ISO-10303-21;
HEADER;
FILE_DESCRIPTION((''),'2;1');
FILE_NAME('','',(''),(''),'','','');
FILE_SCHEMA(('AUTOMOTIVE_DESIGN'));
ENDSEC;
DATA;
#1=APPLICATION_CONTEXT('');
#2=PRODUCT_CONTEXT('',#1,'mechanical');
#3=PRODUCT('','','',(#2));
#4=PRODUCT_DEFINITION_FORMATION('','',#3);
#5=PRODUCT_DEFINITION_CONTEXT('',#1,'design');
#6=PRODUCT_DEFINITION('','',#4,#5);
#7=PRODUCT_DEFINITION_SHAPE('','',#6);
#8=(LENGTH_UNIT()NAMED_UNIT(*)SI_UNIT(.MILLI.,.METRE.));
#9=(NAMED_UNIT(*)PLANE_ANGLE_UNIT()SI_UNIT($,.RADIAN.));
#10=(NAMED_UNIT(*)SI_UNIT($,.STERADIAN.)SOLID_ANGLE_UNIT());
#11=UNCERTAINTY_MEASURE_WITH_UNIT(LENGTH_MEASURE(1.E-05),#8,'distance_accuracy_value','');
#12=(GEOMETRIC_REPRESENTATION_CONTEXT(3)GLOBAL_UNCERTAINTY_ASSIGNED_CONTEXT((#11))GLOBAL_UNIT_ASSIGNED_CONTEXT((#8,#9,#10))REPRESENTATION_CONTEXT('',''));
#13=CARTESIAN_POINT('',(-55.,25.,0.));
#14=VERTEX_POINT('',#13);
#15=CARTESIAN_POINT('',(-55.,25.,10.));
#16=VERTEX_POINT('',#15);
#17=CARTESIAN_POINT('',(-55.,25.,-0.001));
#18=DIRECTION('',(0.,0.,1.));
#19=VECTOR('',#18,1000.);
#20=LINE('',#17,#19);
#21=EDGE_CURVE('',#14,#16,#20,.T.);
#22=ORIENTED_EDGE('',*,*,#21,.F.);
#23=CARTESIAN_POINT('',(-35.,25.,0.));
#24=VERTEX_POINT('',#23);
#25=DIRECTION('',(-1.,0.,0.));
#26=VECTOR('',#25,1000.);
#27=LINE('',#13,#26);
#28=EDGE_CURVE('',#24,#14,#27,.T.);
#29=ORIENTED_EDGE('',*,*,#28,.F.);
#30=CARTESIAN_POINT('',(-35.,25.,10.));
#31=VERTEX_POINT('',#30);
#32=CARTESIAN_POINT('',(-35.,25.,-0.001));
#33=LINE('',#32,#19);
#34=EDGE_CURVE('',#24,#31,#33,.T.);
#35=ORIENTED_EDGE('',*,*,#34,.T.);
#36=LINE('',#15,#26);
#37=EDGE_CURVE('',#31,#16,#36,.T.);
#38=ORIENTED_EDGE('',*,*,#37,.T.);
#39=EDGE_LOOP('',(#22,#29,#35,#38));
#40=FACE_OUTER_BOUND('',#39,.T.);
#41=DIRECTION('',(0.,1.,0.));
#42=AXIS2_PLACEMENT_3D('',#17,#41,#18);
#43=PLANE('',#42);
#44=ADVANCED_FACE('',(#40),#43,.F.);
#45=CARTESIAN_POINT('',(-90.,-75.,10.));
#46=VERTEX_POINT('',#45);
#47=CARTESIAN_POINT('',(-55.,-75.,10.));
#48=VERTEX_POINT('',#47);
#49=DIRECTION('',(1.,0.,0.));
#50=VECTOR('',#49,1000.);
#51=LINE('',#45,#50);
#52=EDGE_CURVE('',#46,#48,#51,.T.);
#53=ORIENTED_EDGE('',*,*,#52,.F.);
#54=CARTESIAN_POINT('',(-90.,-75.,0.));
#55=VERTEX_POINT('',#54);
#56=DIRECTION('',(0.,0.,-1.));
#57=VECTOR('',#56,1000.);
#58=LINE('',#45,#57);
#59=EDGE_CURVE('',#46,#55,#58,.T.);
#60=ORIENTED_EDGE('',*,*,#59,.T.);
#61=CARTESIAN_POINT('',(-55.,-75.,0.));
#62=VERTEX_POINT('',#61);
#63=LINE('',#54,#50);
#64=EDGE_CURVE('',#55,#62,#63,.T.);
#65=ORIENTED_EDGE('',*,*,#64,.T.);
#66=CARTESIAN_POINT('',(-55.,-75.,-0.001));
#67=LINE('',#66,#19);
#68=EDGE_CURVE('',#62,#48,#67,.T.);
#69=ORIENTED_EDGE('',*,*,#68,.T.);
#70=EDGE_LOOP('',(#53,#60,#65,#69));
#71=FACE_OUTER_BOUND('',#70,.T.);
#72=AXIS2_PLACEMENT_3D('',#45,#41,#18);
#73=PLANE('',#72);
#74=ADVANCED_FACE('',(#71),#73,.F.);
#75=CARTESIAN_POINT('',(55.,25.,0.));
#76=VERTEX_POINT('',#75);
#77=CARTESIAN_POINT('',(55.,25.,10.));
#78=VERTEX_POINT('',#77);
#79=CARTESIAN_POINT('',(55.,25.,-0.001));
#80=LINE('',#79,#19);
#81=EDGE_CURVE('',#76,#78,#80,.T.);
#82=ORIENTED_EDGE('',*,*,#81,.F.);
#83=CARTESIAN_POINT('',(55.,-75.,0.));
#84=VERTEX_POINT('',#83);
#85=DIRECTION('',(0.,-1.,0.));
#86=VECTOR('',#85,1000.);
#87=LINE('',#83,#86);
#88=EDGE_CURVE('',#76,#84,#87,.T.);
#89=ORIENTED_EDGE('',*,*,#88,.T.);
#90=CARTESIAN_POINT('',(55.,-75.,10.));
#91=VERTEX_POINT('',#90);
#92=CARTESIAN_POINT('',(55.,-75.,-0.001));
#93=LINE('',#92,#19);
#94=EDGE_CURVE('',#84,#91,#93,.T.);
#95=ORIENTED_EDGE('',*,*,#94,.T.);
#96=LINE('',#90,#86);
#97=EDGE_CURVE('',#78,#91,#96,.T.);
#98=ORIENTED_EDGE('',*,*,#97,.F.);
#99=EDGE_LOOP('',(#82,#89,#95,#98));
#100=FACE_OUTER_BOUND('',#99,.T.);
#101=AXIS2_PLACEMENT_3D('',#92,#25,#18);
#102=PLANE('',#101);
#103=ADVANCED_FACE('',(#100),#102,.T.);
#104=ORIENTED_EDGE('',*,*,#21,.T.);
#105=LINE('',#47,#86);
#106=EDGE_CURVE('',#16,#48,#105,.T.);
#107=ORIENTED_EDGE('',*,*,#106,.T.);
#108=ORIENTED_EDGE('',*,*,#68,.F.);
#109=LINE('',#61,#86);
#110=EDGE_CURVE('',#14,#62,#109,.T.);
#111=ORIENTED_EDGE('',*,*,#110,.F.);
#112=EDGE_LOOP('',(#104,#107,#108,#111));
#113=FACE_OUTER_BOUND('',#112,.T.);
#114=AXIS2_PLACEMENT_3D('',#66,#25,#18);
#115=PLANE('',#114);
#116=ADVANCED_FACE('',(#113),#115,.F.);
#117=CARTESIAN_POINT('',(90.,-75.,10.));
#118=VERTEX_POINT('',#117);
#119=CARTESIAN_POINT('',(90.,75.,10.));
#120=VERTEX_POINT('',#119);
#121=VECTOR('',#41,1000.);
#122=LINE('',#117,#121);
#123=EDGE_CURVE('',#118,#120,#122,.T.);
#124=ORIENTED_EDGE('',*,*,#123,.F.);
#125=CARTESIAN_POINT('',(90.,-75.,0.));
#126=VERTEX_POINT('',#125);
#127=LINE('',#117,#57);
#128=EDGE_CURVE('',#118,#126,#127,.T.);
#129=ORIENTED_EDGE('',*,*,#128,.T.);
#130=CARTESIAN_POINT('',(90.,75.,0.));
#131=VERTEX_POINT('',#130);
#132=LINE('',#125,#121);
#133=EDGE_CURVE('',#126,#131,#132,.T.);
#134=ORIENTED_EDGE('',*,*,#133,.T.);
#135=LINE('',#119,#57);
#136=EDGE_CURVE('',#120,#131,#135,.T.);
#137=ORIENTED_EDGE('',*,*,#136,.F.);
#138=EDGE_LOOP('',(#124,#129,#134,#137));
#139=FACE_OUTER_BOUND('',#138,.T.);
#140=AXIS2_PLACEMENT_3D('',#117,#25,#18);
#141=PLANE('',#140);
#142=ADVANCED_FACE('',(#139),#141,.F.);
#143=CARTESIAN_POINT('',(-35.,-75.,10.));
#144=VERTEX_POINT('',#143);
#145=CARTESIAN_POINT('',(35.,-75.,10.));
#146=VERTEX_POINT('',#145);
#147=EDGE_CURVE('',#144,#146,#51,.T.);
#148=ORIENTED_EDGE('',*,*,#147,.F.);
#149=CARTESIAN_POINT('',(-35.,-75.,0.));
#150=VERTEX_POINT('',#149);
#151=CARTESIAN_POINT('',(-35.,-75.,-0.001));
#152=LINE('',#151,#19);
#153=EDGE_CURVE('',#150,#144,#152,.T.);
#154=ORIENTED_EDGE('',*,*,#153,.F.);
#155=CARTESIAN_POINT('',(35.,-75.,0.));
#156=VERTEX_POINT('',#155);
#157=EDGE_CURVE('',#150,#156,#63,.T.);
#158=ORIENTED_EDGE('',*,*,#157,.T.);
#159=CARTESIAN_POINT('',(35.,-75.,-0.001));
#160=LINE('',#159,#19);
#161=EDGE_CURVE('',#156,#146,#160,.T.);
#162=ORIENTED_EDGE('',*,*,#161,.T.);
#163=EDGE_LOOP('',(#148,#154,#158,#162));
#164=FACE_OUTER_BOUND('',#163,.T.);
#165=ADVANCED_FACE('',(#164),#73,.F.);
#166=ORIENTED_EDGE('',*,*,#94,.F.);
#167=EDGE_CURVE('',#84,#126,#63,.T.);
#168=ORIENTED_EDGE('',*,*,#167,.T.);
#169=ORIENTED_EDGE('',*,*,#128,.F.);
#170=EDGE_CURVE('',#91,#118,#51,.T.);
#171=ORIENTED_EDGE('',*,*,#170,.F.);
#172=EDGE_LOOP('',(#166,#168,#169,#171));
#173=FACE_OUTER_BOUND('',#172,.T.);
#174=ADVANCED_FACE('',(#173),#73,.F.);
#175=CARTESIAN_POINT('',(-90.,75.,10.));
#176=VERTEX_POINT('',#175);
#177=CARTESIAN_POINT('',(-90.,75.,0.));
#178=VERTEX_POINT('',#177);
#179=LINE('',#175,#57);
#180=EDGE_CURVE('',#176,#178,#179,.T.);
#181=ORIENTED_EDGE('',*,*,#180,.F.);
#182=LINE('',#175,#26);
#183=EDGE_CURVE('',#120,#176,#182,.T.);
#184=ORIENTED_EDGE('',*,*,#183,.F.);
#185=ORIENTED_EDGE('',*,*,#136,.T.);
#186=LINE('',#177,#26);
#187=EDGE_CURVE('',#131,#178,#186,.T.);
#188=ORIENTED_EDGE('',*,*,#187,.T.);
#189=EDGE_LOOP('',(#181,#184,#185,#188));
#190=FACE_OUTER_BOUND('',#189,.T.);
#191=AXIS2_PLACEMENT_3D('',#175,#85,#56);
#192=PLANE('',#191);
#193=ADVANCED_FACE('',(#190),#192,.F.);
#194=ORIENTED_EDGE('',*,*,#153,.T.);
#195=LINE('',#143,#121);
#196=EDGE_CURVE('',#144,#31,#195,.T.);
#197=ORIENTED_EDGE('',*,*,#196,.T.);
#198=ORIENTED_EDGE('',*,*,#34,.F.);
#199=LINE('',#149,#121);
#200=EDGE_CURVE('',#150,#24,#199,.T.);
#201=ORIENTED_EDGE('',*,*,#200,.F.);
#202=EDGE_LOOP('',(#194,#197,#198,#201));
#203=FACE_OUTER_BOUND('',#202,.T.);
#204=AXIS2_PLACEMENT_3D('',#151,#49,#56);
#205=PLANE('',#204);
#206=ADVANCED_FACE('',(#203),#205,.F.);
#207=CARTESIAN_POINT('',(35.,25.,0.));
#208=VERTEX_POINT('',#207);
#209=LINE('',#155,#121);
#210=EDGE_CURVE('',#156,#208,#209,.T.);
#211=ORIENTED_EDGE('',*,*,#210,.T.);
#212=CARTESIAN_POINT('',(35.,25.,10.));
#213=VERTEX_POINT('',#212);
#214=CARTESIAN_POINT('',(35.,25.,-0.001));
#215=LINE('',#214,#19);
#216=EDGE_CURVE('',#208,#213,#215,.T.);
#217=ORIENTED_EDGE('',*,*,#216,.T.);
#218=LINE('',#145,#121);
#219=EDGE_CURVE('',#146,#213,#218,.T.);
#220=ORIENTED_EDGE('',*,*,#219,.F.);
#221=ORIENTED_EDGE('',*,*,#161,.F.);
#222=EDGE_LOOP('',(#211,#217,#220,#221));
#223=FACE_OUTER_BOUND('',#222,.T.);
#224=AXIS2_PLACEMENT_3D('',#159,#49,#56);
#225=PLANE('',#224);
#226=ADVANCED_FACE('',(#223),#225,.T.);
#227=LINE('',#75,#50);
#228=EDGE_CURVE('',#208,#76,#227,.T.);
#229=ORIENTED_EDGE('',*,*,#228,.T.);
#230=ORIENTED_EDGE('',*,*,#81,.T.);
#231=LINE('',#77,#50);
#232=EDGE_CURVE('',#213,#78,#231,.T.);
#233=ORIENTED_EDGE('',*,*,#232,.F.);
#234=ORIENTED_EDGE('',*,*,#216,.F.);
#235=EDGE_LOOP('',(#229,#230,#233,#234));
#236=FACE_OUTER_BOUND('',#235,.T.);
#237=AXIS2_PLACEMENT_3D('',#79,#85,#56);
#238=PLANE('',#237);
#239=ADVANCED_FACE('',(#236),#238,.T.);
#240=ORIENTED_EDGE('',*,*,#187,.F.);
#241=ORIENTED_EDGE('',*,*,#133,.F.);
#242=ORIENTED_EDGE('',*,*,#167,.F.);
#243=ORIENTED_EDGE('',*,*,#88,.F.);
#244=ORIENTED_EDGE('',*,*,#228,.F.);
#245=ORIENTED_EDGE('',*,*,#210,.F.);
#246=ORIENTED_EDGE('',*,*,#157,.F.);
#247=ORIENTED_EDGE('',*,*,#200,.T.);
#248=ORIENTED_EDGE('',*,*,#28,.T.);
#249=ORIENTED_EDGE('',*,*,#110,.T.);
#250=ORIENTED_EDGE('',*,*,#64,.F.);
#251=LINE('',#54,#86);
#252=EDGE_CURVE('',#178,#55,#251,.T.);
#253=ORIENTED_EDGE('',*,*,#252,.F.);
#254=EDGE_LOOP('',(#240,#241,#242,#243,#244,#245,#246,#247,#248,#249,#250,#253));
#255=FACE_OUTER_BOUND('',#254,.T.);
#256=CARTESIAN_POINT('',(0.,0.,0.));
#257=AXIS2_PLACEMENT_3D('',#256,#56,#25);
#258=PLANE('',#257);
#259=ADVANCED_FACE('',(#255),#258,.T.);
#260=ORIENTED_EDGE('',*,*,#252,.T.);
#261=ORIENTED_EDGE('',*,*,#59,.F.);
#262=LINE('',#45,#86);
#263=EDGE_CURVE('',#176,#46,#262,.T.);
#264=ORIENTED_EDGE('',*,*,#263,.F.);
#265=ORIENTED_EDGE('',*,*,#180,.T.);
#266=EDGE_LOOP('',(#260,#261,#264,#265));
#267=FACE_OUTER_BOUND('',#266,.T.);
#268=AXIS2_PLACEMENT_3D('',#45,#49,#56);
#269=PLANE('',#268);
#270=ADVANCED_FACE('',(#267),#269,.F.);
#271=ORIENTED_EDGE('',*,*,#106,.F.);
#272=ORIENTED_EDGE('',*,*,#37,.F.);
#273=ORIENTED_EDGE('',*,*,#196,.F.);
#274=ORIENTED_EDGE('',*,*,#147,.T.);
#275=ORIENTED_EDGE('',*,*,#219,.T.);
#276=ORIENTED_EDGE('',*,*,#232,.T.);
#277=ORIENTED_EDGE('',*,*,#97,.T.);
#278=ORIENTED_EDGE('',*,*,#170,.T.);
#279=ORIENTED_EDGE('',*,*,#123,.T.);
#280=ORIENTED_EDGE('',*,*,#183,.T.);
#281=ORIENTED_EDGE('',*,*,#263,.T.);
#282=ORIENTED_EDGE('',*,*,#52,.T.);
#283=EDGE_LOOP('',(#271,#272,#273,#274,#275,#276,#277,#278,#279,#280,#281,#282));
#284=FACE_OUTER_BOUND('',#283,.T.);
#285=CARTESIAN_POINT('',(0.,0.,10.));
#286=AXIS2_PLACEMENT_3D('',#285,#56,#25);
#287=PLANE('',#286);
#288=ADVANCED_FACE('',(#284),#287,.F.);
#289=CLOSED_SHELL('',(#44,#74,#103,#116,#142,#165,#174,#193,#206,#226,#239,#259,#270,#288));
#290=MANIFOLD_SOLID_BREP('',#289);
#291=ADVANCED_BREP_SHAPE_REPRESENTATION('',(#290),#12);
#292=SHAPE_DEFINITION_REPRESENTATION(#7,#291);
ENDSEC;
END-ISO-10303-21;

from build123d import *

# Parameters (mm, degrees)
SKETCH_1_W          = 180
SKETCH_1_H          = 150
EXTRUDE_1_DEPTH     = 10
CUT_EXTRUDE_1_REACH = 119.58
SKETCH_2_W          = 20
SKETCH_2_H          = 100


with BuildPart() as part:
    # 草图1 → 凸台-拉伸1 (new body)
    with BuildSketch(Plane.XY):
        Rectangle(SKETCH_1_W, SKETCH_1_H)
    extrude(amount=EXTRUDE_1_DEPTH)

    # 草图2 → 切除-拉伸1 (cut, up to next)
    with BuildSketch(Plane.XY.offset(10), mode=Mode.PRIVATE) as cut_extrude_1_sk1:
        with Locations((-45, -25)):
            Rectangle(SKETCH_2_W, SKETCH_2_H)
    cut_extrude_1_tool1 = extrude(cut_extrude_1_sk1.sketch, amount=-CUT_EXTRUDE_1_REACH, mode=Mode.PRIVATE) & part.part
    cut_extrude_1 = cut_extrude_1_tool1.solids().sort_by_distance((-45, -25, 10))[0]
    add(cut_extrude_1, mode=Mode.SUBTRACT)

    # 镜向1: 切除-拉伸1 across plane
    add(cut_extrude_1.mirror(Plane(origin=(0, 0, 0), x_dir=(0, 0, 1), z_dir=(1, 0, 0))), mode=Mode.SUBTRACT)


solid = part.part
